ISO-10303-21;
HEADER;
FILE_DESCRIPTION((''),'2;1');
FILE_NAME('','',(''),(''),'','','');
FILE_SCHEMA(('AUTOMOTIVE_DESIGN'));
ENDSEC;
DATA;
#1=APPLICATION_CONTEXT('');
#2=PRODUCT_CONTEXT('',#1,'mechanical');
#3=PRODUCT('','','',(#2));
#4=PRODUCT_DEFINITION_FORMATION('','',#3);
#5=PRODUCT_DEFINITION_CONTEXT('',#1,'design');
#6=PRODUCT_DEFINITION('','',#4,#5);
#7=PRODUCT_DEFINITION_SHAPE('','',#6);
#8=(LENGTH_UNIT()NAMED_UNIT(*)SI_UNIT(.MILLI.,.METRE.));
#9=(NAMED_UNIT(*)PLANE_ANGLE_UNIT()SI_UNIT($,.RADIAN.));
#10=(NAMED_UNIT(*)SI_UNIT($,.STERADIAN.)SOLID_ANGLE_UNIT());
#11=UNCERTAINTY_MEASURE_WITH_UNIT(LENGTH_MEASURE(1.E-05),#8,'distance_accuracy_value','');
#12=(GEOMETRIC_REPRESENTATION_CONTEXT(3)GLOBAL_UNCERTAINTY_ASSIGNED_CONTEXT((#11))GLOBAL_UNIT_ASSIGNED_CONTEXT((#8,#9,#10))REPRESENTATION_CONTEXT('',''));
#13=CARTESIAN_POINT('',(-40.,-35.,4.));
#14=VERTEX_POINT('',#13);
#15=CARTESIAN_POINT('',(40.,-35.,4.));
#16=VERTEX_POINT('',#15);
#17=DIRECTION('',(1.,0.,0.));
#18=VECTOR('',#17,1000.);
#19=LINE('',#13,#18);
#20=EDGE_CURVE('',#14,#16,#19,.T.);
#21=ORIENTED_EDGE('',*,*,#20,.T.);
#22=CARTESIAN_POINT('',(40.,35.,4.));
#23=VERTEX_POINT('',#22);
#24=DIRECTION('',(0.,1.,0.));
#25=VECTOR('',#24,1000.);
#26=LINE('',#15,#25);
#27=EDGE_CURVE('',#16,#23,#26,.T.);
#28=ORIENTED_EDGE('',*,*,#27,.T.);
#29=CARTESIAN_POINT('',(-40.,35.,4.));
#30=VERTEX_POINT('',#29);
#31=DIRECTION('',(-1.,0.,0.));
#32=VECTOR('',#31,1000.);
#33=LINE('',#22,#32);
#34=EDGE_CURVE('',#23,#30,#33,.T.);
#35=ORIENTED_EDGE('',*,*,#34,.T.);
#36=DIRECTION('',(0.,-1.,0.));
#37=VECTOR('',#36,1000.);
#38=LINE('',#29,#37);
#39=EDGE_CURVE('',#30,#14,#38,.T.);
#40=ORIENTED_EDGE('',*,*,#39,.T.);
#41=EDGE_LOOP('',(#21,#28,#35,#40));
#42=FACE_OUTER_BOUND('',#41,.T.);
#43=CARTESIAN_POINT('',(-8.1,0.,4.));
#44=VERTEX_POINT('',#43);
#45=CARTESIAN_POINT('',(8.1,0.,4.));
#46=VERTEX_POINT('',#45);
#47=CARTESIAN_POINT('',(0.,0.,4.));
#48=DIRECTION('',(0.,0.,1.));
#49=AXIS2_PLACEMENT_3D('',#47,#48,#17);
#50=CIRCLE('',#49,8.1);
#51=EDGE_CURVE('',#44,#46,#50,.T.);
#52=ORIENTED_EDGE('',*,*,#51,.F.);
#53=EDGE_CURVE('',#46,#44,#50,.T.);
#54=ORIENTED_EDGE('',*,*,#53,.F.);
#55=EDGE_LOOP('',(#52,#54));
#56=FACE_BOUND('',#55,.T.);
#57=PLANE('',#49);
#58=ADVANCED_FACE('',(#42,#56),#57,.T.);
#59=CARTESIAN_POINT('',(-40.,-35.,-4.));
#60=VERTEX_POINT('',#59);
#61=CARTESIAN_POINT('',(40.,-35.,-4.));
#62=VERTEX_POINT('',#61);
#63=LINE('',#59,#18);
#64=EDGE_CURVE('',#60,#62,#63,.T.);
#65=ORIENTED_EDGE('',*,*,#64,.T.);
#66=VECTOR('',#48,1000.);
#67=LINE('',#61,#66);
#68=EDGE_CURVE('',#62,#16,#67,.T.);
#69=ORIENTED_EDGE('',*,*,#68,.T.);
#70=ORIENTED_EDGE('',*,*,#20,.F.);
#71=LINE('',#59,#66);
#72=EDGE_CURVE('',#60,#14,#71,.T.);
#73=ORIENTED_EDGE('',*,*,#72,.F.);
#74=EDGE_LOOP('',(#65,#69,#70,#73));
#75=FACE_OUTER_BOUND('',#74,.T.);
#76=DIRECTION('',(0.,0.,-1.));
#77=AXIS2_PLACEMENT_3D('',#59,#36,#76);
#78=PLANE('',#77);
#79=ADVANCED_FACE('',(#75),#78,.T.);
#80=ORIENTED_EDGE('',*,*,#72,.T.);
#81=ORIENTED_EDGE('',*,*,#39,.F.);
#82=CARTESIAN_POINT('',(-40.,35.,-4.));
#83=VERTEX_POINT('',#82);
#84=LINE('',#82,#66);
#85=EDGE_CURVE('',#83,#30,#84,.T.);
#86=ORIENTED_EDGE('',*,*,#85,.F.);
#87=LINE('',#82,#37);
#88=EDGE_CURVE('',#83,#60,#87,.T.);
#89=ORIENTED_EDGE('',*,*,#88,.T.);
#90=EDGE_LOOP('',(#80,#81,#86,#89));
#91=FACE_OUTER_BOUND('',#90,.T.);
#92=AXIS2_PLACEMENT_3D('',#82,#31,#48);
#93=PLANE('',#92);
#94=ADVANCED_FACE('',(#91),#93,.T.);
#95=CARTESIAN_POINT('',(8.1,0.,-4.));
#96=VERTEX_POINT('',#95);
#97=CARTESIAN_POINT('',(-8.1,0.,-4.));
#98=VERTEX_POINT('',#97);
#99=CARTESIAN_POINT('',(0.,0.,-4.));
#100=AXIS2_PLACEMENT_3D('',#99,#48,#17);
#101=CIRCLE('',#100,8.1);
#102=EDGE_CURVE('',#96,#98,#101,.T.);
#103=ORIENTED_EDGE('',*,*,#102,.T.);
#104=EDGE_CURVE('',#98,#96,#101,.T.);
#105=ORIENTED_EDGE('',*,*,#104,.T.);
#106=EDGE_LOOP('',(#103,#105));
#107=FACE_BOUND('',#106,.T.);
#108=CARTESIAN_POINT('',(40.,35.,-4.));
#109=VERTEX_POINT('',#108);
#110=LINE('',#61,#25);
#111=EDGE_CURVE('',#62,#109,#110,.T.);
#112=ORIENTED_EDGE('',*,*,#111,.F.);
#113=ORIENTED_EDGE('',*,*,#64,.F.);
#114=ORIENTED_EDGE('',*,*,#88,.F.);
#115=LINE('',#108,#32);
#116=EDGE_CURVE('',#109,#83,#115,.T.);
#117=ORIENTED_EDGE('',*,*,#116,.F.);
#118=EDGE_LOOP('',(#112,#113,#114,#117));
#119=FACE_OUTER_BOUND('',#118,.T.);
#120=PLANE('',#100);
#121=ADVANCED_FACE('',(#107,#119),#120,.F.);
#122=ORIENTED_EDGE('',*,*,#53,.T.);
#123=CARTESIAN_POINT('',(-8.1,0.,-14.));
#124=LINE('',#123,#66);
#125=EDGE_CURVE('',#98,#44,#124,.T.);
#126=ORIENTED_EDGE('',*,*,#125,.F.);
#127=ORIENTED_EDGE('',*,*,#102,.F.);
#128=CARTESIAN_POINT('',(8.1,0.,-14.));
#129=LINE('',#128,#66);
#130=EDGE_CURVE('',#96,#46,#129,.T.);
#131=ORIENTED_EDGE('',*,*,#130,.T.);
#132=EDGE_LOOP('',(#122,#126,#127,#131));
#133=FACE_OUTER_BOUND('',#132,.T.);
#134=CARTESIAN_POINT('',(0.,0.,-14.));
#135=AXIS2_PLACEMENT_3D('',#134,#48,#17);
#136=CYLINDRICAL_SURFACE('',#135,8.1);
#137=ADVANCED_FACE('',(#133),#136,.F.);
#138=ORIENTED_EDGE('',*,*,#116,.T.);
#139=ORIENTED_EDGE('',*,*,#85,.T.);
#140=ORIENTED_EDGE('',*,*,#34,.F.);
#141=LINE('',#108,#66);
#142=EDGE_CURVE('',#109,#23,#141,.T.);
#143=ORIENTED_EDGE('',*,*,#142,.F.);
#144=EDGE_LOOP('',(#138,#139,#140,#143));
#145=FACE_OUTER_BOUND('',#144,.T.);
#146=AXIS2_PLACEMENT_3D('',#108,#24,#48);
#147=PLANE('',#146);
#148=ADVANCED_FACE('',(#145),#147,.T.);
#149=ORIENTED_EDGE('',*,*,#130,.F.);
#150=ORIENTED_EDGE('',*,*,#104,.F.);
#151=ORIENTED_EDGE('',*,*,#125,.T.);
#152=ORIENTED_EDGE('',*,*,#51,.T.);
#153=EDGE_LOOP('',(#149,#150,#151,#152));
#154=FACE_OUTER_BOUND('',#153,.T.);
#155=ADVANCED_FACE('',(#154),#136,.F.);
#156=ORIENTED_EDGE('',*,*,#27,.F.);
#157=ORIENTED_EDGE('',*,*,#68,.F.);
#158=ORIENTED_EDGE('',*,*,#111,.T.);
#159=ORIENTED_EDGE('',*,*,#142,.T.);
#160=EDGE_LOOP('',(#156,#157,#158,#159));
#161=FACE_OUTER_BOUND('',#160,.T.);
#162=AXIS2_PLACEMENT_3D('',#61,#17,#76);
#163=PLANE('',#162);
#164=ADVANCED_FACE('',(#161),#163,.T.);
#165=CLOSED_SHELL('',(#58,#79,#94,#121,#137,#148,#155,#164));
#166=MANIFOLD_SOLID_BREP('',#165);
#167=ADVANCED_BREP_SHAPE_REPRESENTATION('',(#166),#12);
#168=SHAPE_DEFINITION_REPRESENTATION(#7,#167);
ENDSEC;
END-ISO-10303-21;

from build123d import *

# Parameters (mm, degrees)
SKETCH_1_W          = 80
SKETCH_1_H          = 70
EXTRUDE_1_DEPTH     = 4
SKETCH_2_R          = 8.1
CUT_EXTRUDE_1_DEPTH = 14


with BuildPart() as part:
    # 草图1 → 凸台-拉伸1 (new, symmetric)
    with BuildSketch(Plane.XY):
        Rectangle(SKETCH_1_W, SKETCH_1_H)
    extrude(amount=EXTRUDE_1_DEPTH, both=True)

    # 草图2 → 切除-拉伸1 (cut, symmetric)
    with BuildSketch(Plane.XY):
        Circle(SKETCH_2_R)
    extrude(amount=CUT_EXTRUDE_1_DEPTH, both=True, mode=Mode.SUBTRACT)


solid = part.part
